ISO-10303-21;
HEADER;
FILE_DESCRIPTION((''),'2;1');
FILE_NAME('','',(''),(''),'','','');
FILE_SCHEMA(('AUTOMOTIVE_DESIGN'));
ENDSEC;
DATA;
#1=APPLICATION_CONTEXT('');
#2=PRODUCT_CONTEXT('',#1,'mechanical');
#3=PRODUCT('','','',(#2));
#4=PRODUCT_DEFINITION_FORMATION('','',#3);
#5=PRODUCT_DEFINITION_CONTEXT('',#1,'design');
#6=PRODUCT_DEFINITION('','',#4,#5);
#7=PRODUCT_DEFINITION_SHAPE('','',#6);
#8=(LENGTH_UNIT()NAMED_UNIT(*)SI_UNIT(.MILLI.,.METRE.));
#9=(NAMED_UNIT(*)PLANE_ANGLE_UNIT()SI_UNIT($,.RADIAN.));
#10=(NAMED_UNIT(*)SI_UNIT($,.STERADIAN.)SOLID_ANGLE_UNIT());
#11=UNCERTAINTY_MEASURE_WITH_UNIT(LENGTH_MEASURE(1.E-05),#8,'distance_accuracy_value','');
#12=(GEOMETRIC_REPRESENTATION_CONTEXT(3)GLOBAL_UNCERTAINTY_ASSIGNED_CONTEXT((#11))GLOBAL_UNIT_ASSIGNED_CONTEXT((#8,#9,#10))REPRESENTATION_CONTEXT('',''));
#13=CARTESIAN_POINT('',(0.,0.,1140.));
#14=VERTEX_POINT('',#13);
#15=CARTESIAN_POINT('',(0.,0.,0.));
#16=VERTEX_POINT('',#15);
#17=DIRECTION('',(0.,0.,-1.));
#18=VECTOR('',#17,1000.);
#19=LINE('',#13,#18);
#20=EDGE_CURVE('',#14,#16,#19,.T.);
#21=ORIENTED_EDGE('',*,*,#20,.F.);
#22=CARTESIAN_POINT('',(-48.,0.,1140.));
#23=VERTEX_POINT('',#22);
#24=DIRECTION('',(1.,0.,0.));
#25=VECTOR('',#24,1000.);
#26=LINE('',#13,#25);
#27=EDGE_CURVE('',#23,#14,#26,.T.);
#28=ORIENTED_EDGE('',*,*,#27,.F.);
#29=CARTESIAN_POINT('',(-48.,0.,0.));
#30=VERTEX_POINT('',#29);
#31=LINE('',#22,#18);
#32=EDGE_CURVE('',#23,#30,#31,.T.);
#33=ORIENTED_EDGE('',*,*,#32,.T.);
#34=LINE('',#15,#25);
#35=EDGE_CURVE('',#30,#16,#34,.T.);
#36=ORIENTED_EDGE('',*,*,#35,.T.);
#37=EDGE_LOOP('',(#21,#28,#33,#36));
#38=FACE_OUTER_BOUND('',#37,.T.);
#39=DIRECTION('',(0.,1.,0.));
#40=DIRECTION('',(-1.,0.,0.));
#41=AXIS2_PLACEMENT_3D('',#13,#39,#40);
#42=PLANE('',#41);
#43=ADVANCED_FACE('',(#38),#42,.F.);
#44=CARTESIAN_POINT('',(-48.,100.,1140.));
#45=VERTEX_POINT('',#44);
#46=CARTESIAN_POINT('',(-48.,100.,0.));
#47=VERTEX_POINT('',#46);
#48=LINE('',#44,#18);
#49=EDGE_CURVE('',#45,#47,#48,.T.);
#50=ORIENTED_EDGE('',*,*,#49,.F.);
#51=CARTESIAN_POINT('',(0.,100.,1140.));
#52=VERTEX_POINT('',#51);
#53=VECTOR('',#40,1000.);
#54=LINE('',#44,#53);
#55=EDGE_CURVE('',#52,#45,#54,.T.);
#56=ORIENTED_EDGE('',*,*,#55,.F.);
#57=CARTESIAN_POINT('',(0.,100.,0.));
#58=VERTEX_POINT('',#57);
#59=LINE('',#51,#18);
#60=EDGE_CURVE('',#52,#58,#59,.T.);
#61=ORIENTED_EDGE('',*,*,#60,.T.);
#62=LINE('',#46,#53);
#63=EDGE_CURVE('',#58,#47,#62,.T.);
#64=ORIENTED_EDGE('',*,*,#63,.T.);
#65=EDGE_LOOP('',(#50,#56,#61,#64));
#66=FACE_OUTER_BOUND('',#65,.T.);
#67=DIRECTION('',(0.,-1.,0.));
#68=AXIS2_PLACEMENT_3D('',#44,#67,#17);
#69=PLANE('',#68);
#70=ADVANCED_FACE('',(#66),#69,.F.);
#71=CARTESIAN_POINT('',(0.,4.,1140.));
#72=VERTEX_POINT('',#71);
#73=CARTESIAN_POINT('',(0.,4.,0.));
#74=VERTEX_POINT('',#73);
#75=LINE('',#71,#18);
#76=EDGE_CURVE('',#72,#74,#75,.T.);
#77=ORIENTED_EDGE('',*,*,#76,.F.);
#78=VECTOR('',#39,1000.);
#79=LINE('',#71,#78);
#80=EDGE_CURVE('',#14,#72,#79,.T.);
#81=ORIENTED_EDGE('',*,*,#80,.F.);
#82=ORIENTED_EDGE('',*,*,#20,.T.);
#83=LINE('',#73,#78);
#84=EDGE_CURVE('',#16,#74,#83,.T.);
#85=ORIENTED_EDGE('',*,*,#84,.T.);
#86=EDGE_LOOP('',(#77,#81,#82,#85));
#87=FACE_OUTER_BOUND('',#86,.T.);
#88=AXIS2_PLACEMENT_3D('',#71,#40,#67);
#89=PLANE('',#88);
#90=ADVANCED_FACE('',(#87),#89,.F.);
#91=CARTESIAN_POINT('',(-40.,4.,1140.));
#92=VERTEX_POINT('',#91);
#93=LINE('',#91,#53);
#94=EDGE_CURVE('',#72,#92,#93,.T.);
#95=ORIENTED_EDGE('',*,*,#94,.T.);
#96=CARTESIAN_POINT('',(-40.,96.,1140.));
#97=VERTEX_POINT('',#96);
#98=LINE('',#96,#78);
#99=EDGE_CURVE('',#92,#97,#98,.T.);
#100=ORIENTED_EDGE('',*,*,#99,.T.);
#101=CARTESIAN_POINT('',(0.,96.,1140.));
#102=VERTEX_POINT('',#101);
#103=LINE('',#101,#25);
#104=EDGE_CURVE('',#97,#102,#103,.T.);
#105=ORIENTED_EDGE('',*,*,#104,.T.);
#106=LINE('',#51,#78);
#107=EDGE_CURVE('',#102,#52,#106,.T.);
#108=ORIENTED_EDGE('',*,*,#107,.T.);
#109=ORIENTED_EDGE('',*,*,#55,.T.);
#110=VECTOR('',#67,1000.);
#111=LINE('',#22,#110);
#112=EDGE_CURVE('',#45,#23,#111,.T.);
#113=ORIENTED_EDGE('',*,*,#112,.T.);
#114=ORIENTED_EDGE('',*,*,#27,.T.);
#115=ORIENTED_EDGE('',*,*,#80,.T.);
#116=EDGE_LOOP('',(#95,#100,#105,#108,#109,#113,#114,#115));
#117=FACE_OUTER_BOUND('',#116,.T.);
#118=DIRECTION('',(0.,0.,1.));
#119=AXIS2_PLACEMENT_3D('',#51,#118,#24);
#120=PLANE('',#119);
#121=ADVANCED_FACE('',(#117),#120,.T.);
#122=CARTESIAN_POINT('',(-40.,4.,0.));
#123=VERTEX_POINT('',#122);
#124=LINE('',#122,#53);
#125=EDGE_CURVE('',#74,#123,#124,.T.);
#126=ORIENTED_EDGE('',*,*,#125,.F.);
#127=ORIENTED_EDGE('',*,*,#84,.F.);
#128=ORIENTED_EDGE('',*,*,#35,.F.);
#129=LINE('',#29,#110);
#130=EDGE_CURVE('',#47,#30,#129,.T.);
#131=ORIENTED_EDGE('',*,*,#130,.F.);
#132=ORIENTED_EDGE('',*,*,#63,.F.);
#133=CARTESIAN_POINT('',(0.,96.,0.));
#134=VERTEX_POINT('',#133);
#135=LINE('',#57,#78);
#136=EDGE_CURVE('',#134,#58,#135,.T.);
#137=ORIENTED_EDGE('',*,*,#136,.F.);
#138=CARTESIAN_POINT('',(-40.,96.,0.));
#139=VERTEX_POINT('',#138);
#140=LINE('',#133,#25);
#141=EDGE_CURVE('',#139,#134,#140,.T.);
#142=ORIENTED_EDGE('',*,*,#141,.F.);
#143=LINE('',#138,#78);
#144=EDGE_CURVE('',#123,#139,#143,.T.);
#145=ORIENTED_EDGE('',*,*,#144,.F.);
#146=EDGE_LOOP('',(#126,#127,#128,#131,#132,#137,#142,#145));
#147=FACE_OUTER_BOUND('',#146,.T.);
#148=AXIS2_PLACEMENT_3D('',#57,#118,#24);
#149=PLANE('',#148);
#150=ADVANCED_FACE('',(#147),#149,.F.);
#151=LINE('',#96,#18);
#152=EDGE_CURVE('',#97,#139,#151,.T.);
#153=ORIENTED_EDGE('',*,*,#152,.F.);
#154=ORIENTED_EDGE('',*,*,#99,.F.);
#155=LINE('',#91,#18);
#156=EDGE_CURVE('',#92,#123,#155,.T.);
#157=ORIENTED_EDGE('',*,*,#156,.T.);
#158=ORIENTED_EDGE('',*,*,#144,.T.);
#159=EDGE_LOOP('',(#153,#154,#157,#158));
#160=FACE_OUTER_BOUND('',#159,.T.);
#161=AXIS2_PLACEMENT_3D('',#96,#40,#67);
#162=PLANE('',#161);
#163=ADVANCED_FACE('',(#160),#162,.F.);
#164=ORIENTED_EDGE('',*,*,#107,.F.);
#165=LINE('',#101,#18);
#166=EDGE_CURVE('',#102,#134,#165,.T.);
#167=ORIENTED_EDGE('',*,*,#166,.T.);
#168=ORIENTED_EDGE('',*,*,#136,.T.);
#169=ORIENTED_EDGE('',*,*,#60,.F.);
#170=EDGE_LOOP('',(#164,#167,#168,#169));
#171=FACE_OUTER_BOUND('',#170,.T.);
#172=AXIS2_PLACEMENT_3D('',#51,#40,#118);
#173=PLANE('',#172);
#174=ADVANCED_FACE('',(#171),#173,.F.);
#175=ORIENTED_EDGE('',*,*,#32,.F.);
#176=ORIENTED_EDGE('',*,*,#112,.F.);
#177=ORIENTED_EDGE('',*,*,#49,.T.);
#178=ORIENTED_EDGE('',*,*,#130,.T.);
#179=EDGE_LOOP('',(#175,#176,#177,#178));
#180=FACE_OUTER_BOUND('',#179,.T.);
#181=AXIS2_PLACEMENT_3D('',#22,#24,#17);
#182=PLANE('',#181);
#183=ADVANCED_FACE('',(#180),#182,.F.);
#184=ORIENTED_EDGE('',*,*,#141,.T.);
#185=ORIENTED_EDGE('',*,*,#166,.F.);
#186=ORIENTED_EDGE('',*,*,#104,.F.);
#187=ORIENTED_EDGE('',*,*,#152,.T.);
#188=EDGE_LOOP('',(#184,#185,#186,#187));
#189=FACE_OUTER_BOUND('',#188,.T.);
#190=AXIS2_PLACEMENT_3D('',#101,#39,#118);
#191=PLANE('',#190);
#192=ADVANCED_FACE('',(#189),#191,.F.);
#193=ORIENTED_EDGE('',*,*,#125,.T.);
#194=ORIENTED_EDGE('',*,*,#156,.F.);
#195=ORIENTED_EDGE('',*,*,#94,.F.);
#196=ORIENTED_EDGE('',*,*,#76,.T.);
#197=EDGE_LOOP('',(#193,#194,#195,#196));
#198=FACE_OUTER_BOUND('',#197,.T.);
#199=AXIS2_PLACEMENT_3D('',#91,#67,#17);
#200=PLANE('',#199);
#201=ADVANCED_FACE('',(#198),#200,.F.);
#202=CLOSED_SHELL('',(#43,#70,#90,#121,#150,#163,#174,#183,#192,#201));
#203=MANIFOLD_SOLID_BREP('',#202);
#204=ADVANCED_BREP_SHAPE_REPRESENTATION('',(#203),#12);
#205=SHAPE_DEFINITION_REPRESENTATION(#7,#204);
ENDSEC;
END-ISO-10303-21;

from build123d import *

# Parameters (mm, degrees)
EXTRUDE1_DEPTH = 1140


with BuildPart() as part:
    # Sketch1 → Extrude1 (new body)
    with BuildSketch(Plane.XY):
        Polygon((0, 0), (-48, 0), (-48, 100), (0, 100), (0, 96), (-40, 96), (-40, 4), (0, 4), align=None)
    extrude(amount=EXTRUDE1_DEPTH)


solid = part.part
